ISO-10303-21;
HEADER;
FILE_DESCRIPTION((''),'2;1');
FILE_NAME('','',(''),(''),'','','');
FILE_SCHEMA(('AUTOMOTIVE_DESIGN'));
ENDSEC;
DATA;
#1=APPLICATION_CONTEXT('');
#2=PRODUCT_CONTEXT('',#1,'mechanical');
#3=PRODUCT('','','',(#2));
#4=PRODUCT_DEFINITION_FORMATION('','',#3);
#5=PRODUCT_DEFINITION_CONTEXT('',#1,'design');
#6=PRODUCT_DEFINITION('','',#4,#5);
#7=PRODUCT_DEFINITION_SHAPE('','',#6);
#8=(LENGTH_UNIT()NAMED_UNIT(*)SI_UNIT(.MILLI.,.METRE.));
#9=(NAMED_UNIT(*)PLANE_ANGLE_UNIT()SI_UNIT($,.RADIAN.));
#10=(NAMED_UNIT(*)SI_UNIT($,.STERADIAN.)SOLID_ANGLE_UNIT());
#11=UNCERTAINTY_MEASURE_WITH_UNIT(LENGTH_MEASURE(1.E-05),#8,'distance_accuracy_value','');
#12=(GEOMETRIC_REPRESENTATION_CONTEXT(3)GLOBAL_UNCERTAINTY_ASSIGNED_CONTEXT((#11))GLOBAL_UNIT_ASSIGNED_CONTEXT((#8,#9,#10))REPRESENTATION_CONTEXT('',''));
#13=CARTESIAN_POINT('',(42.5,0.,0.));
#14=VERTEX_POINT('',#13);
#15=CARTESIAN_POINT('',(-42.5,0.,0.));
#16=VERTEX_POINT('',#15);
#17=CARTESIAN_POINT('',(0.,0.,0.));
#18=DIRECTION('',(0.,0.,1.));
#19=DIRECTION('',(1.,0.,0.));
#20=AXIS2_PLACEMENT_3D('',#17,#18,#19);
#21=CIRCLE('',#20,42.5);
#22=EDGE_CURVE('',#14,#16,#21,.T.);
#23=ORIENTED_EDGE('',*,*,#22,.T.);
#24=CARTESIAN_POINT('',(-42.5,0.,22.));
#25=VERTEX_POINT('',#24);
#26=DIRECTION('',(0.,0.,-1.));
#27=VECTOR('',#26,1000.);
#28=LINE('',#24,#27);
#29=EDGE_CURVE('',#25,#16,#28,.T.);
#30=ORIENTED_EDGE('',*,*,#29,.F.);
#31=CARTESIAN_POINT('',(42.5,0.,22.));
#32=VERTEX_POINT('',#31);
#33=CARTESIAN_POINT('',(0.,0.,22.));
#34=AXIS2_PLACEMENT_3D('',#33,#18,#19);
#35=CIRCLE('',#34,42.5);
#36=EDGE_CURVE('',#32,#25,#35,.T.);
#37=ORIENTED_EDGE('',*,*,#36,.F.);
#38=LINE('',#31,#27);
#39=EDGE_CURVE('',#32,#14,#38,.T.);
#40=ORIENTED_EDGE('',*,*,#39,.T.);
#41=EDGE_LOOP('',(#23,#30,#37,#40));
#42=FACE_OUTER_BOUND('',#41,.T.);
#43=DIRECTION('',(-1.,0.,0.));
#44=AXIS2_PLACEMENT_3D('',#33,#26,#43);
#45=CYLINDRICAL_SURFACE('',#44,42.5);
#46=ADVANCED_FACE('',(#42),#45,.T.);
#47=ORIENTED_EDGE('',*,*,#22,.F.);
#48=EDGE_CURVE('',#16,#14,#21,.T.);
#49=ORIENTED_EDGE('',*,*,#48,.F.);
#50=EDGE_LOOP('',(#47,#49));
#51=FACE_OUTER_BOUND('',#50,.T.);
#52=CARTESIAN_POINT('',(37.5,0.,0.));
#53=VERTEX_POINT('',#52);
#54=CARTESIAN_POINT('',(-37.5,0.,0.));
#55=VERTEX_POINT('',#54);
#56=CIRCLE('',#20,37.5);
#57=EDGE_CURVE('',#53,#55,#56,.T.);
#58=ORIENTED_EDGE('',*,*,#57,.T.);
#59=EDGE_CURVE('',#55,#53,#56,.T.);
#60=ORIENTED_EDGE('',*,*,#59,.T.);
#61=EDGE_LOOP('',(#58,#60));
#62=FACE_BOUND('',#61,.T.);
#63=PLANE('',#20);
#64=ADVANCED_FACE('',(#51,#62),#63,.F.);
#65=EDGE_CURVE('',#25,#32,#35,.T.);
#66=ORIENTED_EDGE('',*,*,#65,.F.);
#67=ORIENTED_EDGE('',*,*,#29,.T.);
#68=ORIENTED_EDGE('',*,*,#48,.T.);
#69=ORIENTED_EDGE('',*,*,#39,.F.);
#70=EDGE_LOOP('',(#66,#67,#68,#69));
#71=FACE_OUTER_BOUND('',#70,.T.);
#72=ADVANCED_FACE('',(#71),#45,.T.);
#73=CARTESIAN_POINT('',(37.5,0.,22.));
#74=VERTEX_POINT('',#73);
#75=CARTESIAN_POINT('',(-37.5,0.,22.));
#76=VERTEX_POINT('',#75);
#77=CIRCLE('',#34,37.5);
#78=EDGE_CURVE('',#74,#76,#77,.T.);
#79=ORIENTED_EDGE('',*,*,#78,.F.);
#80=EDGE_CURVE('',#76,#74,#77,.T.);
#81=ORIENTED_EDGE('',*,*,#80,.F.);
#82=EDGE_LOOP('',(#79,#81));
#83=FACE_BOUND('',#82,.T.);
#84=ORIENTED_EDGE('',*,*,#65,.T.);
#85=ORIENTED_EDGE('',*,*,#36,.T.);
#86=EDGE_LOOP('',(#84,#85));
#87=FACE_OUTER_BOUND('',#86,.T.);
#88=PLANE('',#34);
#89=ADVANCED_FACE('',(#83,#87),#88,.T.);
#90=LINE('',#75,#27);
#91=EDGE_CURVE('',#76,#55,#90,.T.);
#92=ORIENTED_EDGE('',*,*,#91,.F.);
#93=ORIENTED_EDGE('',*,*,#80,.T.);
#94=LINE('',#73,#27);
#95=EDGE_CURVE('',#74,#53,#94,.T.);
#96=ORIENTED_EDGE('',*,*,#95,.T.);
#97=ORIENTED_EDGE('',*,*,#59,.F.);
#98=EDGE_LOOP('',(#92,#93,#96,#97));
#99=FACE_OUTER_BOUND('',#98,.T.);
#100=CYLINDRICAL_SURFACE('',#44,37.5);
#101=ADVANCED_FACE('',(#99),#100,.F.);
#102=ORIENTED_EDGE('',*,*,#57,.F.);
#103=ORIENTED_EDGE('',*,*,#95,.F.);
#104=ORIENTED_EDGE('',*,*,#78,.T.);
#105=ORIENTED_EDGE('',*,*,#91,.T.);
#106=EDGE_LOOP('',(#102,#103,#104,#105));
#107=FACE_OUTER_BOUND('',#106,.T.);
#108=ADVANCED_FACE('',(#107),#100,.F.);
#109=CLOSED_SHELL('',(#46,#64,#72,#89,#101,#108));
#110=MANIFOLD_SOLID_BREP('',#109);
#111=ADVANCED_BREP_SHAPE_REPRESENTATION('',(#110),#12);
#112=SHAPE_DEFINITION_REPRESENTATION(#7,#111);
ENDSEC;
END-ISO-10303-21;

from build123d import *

# Parameters (mm, degrees)
SKETCH_1_R      = 42.5
SKETCH_1_R_2    = 37.5
EXTRUDE_1_DEPTH = 22


with BuildPart() as part:
    # 草图1 → 凸台-拉伸1 (new body)
    with BuildSketch(Plane.XY):
        Circle(SKETCH_1_R)
        Circle(SKETCH_1_R_2, mode=Mode.SUBTRACT)
    extrude(amount=EXTRUDE_1_DEPTH)


solid = part.part
